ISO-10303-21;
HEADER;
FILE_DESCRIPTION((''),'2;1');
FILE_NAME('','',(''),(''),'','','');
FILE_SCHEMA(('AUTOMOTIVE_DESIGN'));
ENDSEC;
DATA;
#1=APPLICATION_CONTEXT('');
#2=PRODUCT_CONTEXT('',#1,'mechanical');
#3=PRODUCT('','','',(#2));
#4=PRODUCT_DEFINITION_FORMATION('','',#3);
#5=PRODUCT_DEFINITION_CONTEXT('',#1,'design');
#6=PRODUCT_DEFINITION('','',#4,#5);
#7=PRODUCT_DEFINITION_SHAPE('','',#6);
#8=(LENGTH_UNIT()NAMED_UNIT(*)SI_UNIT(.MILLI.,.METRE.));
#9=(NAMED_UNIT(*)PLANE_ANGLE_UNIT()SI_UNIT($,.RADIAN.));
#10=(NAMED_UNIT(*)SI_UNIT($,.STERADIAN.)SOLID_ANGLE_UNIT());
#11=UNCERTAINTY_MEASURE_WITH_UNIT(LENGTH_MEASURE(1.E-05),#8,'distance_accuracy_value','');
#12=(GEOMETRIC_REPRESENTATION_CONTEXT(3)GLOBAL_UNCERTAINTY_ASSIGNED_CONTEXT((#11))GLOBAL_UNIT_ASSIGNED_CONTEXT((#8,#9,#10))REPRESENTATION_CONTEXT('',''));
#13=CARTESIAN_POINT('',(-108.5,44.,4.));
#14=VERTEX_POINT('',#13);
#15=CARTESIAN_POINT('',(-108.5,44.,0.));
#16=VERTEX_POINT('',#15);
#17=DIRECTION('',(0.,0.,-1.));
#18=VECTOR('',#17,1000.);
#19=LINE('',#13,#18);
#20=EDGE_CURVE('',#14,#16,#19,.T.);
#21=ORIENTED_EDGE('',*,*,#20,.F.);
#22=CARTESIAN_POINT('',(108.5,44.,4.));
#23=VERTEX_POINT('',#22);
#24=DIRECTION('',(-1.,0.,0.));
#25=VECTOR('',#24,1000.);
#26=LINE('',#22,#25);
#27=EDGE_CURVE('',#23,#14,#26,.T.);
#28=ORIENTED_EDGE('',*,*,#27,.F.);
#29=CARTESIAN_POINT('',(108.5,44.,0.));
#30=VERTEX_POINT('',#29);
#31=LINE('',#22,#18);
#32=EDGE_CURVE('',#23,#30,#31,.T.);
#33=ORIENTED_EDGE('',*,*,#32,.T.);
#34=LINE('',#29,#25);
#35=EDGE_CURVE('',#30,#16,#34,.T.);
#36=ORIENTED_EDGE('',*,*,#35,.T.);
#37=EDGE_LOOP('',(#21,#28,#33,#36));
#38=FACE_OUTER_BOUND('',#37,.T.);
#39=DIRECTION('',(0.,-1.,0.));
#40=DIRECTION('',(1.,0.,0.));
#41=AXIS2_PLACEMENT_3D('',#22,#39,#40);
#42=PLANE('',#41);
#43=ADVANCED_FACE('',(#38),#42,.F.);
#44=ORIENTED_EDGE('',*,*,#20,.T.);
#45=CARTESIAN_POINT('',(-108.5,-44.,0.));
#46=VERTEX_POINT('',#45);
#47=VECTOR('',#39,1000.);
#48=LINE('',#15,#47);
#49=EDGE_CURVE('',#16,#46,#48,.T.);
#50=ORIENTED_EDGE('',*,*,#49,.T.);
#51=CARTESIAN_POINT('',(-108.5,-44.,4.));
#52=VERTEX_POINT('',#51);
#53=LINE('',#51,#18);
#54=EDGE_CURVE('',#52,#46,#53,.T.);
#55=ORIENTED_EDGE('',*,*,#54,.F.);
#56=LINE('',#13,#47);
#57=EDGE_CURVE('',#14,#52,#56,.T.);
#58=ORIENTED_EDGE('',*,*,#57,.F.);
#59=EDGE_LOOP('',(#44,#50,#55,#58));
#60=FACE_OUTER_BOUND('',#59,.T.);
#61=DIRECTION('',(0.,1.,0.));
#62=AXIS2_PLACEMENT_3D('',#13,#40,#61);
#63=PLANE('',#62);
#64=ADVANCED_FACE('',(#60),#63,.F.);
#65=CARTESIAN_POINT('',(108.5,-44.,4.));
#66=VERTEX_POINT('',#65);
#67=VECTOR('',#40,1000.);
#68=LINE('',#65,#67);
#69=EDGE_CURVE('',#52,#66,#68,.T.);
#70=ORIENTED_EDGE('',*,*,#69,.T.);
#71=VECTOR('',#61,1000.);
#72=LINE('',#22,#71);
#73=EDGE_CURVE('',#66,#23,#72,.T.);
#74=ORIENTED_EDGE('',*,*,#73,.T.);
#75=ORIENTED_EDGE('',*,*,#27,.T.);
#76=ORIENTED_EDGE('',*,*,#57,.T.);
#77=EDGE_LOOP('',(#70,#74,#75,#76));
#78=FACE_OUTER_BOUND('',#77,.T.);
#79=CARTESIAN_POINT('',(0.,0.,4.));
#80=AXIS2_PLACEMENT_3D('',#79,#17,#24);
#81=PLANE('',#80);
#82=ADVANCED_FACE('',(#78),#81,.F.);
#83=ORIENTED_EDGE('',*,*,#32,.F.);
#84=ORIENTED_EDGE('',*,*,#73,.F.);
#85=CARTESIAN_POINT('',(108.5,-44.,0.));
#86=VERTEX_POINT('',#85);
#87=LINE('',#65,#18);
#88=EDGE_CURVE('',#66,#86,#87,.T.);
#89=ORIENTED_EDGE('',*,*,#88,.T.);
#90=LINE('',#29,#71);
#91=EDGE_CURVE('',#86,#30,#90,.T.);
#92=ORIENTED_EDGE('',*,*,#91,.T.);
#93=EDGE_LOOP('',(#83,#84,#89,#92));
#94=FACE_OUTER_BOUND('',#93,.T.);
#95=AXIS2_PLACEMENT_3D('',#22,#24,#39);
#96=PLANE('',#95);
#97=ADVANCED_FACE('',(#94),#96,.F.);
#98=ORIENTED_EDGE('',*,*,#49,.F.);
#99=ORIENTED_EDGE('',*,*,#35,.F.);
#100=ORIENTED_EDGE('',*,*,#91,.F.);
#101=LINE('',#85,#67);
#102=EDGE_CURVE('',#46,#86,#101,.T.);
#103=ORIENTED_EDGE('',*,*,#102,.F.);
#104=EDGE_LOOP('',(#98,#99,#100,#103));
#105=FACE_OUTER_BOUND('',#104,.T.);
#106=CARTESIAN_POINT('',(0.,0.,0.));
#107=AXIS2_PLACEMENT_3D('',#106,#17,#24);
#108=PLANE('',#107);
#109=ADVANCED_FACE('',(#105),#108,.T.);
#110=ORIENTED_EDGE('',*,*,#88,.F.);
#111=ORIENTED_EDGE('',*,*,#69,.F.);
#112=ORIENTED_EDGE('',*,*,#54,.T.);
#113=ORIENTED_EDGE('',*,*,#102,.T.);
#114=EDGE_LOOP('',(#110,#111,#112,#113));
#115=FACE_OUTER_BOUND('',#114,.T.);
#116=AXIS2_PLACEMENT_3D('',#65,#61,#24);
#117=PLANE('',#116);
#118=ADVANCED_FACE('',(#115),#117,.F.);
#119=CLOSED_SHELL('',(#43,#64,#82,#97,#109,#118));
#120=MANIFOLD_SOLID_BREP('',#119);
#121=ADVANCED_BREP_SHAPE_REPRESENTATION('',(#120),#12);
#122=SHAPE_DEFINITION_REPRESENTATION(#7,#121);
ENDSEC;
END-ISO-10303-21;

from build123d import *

# Parameters (mm, degrees)
SKETCH_1_W      = 217
SKETCH_1_H      = 88
EXTRUDE_1_DEPTH = 4


with BuildPart() as part:
    # 草图1 → 凸台-拉伸1 (new body)
    with BuildSketch(Plane.XY):
        Rectangle(SKETCH_1_W, SKETCH_1_H)
    extrude(amount=EXTRUDE_1_DEPTH)


solid = part.part
